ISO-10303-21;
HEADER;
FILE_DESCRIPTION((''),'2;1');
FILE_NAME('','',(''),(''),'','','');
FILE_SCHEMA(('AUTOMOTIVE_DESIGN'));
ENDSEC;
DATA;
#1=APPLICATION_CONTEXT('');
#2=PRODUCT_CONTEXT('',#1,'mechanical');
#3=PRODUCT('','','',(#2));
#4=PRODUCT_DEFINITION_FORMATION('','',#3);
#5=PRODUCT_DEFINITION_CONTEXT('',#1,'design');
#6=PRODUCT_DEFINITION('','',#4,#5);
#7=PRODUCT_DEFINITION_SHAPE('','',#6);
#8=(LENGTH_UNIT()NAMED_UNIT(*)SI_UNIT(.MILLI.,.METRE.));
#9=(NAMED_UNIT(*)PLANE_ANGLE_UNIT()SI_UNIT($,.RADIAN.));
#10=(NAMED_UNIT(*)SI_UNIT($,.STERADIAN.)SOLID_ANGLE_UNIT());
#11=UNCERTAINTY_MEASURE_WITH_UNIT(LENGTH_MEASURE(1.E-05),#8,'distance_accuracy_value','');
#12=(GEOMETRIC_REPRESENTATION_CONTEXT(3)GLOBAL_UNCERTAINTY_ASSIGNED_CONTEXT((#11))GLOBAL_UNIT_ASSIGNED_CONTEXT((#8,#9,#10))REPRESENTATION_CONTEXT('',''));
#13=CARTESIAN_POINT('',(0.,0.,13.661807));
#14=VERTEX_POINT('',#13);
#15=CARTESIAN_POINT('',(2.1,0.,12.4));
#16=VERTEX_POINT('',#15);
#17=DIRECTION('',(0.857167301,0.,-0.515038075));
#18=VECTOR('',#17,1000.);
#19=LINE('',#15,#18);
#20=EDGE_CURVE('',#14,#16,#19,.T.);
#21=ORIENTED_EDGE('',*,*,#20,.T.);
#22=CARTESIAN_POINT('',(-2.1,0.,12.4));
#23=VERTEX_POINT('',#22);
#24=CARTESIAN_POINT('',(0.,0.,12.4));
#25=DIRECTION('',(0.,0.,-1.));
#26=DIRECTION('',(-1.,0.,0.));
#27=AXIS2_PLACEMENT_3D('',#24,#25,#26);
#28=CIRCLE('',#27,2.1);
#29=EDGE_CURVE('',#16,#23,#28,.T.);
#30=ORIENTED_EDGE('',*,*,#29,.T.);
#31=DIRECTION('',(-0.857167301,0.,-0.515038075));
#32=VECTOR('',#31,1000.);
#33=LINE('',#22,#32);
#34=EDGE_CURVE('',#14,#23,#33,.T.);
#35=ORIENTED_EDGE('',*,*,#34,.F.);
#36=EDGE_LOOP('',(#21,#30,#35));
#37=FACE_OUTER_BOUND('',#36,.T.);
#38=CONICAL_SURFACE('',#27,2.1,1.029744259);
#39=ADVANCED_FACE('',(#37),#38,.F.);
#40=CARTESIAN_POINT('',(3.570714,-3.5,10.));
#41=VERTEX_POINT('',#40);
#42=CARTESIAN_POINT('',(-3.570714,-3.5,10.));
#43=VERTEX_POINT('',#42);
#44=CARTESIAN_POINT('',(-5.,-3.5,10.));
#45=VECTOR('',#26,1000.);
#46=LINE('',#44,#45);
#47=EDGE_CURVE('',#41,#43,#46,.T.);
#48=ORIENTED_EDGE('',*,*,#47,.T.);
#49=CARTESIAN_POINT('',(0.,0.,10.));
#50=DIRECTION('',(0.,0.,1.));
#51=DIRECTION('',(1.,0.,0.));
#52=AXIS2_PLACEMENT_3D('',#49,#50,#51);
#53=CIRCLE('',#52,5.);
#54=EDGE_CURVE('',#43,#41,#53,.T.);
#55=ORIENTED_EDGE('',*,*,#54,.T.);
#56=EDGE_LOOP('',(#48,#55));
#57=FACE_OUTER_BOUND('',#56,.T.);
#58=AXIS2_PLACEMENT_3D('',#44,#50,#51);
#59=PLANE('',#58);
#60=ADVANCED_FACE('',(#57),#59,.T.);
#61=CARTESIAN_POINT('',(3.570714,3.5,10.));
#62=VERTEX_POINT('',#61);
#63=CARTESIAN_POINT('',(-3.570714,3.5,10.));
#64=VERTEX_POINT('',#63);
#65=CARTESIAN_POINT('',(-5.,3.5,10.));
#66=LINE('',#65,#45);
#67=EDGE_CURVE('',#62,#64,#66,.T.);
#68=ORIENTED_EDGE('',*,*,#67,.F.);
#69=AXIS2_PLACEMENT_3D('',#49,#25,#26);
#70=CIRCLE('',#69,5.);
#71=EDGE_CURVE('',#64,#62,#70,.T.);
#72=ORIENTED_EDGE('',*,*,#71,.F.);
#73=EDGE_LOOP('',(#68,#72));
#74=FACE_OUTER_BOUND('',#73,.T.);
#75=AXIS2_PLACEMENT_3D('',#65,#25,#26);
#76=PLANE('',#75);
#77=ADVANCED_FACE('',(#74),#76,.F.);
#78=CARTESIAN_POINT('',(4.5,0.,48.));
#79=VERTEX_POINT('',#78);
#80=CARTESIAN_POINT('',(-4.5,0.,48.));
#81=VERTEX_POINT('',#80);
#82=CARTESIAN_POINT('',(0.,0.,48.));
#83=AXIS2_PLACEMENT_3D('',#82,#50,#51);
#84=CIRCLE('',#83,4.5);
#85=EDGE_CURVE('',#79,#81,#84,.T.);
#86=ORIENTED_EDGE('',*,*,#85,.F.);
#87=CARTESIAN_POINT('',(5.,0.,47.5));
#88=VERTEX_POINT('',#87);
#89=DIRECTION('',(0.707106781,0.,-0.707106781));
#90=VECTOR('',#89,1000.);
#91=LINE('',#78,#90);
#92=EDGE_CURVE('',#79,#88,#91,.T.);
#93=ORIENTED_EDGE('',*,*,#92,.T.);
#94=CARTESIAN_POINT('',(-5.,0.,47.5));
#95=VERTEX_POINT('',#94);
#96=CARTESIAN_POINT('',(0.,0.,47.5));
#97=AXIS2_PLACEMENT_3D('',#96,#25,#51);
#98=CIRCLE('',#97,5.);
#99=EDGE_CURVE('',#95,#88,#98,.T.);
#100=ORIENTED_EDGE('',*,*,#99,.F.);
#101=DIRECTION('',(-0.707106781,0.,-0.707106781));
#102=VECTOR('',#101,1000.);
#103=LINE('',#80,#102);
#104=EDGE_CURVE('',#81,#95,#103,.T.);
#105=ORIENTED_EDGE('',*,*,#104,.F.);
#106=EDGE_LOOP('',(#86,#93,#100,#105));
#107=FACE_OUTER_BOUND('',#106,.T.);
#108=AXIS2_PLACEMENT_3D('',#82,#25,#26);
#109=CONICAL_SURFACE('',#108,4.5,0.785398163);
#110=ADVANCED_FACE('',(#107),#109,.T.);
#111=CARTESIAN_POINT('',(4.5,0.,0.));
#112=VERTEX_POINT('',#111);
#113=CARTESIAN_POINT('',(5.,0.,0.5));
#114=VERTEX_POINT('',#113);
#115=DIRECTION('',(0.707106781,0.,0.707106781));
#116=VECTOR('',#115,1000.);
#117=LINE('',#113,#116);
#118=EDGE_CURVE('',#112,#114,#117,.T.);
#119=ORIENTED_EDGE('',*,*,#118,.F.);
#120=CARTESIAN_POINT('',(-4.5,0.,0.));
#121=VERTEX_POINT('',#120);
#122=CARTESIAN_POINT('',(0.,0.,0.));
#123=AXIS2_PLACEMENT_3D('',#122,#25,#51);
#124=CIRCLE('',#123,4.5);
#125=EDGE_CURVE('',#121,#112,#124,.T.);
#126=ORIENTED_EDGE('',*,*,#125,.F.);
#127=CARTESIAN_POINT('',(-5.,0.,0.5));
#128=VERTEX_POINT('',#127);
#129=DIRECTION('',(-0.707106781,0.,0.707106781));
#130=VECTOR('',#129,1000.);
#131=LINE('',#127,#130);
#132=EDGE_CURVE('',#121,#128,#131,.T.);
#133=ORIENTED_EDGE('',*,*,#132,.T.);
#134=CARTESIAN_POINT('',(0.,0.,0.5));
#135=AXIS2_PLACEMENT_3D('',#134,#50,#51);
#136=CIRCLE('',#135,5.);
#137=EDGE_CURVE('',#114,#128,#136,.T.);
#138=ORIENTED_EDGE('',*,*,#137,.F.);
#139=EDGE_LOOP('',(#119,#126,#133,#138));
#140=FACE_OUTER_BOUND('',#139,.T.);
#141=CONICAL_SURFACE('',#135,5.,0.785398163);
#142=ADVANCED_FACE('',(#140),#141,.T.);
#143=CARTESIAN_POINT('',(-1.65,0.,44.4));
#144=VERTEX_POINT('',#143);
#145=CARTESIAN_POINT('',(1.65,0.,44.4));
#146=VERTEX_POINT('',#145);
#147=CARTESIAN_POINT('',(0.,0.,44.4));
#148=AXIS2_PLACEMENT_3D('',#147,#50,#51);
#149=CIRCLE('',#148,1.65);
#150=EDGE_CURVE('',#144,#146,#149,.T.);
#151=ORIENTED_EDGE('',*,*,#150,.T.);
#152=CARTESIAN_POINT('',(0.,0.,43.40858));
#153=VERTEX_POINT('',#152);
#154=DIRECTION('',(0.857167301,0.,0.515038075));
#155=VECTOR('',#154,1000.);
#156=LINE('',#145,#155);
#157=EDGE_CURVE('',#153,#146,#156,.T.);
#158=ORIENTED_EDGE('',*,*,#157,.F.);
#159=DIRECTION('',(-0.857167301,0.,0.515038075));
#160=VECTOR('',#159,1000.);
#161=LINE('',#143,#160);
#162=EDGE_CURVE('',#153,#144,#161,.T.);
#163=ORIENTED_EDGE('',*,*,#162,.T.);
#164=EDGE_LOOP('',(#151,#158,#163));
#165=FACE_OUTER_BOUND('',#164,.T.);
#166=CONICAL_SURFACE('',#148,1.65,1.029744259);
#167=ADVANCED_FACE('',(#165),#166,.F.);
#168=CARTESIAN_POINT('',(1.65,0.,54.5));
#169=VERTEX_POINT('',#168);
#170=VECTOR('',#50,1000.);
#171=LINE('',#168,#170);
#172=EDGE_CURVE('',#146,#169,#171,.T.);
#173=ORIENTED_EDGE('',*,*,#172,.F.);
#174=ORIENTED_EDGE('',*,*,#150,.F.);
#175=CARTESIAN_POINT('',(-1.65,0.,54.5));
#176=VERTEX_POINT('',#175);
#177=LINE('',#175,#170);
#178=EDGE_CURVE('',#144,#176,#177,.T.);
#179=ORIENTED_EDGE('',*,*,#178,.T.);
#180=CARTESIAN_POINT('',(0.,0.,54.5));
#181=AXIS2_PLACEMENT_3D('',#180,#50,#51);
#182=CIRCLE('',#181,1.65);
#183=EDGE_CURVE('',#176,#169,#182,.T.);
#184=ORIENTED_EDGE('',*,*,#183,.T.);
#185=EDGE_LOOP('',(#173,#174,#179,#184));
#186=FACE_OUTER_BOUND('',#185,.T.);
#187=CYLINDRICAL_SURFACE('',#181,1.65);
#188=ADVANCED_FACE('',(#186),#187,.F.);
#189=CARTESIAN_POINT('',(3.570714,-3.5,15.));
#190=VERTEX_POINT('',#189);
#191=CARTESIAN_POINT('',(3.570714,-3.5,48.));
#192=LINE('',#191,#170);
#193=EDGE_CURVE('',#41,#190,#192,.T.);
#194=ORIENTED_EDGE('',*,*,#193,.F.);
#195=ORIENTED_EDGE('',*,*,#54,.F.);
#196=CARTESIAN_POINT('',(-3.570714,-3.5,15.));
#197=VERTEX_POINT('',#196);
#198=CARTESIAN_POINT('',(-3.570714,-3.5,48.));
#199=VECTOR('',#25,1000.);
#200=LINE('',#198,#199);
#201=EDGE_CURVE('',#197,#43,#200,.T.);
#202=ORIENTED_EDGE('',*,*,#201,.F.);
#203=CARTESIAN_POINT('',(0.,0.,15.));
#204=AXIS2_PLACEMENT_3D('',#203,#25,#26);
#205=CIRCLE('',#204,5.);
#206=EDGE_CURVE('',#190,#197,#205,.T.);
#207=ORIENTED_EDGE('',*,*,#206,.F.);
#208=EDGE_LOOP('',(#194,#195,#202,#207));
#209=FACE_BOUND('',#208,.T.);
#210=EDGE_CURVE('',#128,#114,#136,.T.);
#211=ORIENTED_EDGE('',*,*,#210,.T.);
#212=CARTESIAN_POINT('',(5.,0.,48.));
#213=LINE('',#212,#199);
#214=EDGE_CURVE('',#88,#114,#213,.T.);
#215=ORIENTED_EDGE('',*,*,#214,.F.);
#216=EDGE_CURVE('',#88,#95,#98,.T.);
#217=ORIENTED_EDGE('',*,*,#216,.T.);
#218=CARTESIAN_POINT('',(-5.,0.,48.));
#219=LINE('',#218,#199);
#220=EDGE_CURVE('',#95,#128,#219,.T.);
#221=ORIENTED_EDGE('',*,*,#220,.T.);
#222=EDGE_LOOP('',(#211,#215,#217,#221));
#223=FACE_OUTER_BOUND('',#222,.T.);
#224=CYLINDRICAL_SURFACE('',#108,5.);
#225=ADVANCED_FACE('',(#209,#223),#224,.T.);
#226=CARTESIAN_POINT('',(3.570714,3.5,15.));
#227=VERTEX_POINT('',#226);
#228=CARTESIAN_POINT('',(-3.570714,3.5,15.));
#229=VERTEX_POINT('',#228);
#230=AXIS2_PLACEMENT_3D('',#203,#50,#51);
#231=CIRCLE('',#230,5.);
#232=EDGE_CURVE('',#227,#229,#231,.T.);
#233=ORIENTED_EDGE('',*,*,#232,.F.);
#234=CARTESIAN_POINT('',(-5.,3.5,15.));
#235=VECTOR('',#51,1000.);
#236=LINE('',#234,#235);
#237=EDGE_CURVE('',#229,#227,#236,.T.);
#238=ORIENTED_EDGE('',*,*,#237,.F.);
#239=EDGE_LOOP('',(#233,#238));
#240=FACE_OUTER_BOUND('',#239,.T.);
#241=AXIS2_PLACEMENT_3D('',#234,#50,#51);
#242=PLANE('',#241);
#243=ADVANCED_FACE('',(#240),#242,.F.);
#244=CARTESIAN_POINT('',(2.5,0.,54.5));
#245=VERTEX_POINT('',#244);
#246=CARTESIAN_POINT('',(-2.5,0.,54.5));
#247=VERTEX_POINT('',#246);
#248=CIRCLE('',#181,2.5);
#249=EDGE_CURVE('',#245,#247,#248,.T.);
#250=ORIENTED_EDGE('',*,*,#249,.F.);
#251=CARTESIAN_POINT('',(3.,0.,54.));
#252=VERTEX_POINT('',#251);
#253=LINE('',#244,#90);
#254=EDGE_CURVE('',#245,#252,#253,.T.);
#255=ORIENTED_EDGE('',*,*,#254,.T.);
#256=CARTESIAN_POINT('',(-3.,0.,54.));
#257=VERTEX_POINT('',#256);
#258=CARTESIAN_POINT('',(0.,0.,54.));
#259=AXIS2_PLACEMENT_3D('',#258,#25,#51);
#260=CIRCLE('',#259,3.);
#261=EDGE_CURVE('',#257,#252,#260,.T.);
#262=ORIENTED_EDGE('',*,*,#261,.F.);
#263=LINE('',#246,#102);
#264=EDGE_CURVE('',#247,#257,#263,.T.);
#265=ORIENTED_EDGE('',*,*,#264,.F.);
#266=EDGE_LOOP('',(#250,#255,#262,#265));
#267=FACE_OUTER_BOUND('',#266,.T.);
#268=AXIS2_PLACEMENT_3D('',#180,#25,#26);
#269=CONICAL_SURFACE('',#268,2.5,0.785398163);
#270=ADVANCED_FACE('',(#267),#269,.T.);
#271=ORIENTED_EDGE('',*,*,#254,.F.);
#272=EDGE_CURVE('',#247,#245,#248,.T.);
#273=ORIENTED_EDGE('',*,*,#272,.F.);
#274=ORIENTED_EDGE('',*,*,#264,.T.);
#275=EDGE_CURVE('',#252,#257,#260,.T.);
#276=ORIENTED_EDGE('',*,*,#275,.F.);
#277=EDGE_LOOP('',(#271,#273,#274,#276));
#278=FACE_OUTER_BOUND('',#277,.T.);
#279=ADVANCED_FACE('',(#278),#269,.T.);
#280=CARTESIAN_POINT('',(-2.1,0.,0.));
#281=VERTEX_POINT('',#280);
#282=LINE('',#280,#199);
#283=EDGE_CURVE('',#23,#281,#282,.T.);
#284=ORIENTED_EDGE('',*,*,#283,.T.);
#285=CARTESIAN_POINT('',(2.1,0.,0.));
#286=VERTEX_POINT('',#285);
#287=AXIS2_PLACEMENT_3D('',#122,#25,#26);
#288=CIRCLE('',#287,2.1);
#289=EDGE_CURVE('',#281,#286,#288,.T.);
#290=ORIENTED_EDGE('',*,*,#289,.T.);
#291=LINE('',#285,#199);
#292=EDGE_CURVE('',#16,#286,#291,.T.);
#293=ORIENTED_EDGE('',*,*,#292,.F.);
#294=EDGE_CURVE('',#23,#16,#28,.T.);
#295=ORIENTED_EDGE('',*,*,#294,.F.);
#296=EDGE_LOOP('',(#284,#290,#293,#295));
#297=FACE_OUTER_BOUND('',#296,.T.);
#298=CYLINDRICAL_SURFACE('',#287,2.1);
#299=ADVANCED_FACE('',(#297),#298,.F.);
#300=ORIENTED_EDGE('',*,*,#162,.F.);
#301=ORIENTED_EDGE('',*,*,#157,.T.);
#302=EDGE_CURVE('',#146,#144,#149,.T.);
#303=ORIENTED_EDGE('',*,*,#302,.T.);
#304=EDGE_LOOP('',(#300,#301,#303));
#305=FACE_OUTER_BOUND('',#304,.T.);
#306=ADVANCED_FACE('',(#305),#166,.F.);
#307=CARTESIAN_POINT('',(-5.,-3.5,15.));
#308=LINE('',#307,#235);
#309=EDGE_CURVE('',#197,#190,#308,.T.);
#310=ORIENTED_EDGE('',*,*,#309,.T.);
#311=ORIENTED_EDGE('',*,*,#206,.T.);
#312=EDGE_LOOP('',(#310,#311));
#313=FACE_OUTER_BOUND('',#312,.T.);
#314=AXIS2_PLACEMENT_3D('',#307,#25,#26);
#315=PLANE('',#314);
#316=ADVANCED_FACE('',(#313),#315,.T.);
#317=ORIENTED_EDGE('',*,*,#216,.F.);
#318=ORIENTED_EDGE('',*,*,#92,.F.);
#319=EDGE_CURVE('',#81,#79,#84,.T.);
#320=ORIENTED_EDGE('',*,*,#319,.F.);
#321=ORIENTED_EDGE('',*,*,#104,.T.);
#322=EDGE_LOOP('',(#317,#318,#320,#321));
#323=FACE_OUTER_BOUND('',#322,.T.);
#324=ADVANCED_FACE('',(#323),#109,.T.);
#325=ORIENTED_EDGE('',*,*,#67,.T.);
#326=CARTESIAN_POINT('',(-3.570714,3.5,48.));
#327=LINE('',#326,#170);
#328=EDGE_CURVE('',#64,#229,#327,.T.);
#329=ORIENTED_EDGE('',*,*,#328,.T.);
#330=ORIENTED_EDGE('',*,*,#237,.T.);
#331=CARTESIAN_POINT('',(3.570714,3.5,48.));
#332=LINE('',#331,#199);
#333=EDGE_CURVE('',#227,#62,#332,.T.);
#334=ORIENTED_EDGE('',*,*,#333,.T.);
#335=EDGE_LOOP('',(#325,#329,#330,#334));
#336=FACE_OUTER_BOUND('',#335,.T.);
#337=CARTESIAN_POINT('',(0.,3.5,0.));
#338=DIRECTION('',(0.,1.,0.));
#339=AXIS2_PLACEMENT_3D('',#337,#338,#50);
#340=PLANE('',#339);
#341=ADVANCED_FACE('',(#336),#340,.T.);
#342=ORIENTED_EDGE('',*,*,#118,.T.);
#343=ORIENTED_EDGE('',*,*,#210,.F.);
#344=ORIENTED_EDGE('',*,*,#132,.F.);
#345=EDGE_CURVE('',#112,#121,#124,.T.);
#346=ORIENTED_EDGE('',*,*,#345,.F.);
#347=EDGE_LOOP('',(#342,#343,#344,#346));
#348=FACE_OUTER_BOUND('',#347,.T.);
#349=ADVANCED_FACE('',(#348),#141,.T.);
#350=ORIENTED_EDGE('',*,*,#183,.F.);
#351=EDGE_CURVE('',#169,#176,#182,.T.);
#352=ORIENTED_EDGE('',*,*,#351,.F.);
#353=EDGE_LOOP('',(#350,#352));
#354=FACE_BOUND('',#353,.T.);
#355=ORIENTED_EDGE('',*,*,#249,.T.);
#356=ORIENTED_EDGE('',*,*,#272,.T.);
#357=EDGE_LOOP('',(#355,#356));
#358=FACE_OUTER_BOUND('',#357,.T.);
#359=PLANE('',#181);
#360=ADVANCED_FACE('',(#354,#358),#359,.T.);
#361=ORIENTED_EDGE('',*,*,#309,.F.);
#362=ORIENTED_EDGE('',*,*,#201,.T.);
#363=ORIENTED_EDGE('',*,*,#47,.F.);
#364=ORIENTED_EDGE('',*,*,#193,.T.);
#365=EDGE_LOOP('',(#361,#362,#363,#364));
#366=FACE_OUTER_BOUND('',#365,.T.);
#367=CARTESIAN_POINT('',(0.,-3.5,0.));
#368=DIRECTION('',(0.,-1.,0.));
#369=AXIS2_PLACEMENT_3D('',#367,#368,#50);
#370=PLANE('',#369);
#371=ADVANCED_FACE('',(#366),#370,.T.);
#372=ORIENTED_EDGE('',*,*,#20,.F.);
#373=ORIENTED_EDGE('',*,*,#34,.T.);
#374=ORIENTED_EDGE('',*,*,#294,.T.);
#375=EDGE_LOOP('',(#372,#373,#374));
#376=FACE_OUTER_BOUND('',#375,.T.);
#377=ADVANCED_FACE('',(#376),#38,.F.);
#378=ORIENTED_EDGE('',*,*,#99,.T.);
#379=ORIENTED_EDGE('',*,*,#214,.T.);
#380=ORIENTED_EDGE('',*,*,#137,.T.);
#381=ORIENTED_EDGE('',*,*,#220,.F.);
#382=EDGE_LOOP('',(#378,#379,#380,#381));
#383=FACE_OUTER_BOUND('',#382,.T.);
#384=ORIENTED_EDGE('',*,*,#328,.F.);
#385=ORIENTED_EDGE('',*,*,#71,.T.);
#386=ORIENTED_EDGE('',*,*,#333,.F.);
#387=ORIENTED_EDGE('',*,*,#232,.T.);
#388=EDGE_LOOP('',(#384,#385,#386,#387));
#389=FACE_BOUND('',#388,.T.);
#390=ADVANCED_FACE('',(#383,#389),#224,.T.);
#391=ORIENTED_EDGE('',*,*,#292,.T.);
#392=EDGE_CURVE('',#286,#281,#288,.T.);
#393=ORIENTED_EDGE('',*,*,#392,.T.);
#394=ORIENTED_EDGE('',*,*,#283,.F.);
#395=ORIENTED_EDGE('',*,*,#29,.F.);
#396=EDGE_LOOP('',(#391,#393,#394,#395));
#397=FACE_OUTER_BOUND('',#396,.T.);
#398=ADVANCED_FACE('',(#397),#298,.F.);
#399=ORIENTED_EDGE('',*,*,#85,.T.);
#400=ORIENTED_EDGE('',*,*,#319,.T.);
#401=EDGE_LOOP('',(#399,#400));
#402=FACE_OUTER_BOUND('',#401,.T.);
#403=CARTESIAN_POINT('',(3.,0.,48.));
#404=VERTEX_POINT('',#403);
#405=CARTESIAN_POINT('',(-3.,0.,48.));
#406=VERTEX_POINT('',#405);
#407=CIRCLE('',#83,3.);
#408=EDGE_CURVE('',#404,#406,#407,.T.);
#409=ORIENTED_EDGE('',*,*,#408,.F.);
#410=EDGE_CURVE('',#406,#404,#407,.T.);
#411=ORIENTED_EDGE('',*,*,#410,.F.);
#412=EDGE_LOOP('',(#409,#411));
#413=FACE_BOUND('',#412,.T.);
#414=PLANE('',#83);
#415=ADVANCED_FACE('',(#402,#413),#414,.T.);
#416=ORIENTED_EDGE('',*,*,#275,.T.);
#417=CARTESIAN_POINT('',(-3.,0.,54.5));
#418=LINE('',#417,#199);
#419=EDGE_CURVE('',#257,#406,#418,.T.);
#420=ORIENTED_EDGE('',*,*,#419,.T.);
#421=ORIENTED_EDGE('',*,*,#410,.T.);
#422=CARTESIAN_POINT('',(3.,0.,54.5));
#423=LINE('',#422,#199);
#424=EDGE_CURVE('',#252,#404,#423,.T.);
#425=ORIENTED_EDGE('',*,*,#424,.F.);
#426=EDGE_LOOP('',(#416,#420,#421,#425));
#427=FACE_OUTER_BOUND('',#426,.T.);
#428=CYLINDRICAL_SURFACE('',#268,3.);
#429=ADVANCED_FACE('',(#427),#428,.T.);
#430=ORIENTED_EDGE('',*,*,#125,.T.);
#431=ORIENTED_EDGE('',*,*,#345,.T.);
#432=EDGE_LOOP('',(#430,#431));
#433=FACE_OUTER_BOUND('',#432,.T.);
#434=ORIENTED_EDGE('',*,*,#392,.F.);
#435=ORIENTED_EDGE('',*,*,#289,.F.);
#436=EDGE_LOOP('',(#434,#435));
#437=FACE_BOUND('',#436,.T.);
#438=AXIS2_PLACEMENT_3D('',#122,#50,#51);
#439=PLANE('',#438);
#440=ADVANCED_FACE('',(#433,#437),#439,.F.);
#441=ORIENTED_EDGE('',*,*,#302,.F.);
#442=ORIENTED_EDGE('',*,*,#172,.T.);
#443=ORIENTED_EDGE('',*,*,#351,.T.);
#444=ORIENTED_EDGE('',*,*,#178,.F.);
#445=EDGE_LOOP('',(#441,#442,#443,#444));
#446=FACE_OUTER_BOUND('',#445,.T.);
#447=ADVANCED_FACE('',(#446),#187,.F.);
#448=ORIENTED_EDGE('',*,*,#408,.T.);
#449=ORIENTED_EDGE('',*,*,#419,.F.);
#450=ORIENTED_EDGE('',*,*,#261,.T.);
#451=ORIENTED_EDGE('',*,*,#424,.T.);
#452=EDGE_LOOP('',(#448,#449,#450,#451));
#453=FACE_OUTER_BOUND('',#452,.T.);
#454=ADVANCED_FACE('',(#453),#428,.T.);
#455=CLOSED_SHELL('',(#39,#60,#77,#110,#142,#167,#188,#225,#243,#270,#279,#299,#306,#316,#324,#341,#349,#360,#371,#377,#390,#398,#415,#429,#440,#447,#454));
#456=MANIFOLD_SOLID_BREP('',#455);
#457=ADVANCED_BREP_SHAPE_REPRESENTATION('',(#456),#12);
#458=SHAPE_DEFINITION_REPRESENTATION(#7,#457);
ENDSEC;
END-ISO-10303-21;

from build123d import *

# Parameters (mm, degrees)
SKETCH1_R             = 5
BOSS_EXTRUDE1_DEPTH   = 48
SKETCH2_R             = 3
BOSS_EXTRUDE2_DEPTH   = 6.5
M4_TAPPED_HOLE1_D     = 3.3
M4_TAPPED_HOLE1_DEPTH = 10.1
M4_TAPPED_HOLE1_TIP   = 0.991420021
M5_TAPPED_HOLE1_D     = 4.2
M5_TAPPED_HOLE1_DEPTH = 12.4
M5_TAPPED_HOLE1_TIP   = 1.2618073
CHAMFER1_SIZE         = 0.5
CUT_EXTRUDE1_START    = 5
SKETCH7_W             = 10
SKETCH7_H             = 5
CUT_EXTRUDE1_DEPTH    = 1.5


with BuildPart() as part:
    # Sketch1 → Boss-Extrude1 (new body)
    with BuildSketch(Plane.XY):
        Circle(SKETCH1_R)
    extrude(amount=BOSS_EXTRUDE1_DEPTH)

    # Sketch2 → Boss-Extrude2 (add)
    with BuildSketch(Plane.XY.offset(48)):
        with Locations(Location((0, 0, 0), (0, 0, 180))):
            Circle(SKETCH2_R)
    extrude(amount=BOSS_EXTRUDE2_DEPTH)

    # M4 Tapped Hole1
    with Locations(Plane.XY.offset(54.5)):
        with Locations((0, 0)):
            Hole(M4_TAPPED_HOLE1_D / 2, depth=M4_TAPPED_HOLE1_DEPTH)
            with Locations((0, 0, -(M4_TAPPED_HOLE1_DEPTH + M4_TAPPED_HOLE1_TIP / 2))):  # 118° drill point
                Cone(0, M4_TAPPED_HOLE1_D / 2, M4_TAPPED_HOLE1_TIP, mode=Mode.SUBTRACT)

    # M5 Tapped Hole1
    with Locations(Plane(origin=(0, 0, 0), x_dir=(-1, 0, 0), z_dir=(0, 0, -1))):
        with Locations((0, 0)):
            Hole(M5_TAPPED_HOLE1_D / 2, depth=M5_TAPPED_HOLE1_DEPTH)
            with Locations((0, 0, -(M5_TAPPED_HOLE1_DEPTH + M5_TAPPED_HOLE1_TIP / 2))):  # 118° drill point
                Cone(0, M5_TAPPED_HOLE1_D / 2, M5_TAPPED_HOLE1_TIP, mode=Mode.SUBTRACT)

    # Chamfer1
    chamfer1_edges = [part.edges().sort_by_distance(p)[0] for p in [
        (-5, 0, 0),
        (-5, 0, 48),
        (3, 0, 54.5),
    ]]
    chamfer(chamfer1_edges, length=CHAMFER1_SIZE)

    # Sketch7 → Cut-Extrude1 (cut, symmetric)
    with BuildSketch(Plane(origin=(0, 0, 0), x_dir=(1, 0, 0), z_dir=(0, 1, 0)).offset(CUT_EXTRUDE1_START)):
        with Locations((0, -12.5)):
            Rectangle(SKETCH7_W, SKETCH7_H)
    cut_extrude1 = extrude(amount=CUT_EXTRUDE1_DEPTH, both=True, mode=Mode.SUBTRACT)

    # Mirror1: Cut-Extrude1 across plane
    add(cut_extrude1.mirror(Plane.ZX), mode=Mode.SUBTRACT)


solid = part.part
